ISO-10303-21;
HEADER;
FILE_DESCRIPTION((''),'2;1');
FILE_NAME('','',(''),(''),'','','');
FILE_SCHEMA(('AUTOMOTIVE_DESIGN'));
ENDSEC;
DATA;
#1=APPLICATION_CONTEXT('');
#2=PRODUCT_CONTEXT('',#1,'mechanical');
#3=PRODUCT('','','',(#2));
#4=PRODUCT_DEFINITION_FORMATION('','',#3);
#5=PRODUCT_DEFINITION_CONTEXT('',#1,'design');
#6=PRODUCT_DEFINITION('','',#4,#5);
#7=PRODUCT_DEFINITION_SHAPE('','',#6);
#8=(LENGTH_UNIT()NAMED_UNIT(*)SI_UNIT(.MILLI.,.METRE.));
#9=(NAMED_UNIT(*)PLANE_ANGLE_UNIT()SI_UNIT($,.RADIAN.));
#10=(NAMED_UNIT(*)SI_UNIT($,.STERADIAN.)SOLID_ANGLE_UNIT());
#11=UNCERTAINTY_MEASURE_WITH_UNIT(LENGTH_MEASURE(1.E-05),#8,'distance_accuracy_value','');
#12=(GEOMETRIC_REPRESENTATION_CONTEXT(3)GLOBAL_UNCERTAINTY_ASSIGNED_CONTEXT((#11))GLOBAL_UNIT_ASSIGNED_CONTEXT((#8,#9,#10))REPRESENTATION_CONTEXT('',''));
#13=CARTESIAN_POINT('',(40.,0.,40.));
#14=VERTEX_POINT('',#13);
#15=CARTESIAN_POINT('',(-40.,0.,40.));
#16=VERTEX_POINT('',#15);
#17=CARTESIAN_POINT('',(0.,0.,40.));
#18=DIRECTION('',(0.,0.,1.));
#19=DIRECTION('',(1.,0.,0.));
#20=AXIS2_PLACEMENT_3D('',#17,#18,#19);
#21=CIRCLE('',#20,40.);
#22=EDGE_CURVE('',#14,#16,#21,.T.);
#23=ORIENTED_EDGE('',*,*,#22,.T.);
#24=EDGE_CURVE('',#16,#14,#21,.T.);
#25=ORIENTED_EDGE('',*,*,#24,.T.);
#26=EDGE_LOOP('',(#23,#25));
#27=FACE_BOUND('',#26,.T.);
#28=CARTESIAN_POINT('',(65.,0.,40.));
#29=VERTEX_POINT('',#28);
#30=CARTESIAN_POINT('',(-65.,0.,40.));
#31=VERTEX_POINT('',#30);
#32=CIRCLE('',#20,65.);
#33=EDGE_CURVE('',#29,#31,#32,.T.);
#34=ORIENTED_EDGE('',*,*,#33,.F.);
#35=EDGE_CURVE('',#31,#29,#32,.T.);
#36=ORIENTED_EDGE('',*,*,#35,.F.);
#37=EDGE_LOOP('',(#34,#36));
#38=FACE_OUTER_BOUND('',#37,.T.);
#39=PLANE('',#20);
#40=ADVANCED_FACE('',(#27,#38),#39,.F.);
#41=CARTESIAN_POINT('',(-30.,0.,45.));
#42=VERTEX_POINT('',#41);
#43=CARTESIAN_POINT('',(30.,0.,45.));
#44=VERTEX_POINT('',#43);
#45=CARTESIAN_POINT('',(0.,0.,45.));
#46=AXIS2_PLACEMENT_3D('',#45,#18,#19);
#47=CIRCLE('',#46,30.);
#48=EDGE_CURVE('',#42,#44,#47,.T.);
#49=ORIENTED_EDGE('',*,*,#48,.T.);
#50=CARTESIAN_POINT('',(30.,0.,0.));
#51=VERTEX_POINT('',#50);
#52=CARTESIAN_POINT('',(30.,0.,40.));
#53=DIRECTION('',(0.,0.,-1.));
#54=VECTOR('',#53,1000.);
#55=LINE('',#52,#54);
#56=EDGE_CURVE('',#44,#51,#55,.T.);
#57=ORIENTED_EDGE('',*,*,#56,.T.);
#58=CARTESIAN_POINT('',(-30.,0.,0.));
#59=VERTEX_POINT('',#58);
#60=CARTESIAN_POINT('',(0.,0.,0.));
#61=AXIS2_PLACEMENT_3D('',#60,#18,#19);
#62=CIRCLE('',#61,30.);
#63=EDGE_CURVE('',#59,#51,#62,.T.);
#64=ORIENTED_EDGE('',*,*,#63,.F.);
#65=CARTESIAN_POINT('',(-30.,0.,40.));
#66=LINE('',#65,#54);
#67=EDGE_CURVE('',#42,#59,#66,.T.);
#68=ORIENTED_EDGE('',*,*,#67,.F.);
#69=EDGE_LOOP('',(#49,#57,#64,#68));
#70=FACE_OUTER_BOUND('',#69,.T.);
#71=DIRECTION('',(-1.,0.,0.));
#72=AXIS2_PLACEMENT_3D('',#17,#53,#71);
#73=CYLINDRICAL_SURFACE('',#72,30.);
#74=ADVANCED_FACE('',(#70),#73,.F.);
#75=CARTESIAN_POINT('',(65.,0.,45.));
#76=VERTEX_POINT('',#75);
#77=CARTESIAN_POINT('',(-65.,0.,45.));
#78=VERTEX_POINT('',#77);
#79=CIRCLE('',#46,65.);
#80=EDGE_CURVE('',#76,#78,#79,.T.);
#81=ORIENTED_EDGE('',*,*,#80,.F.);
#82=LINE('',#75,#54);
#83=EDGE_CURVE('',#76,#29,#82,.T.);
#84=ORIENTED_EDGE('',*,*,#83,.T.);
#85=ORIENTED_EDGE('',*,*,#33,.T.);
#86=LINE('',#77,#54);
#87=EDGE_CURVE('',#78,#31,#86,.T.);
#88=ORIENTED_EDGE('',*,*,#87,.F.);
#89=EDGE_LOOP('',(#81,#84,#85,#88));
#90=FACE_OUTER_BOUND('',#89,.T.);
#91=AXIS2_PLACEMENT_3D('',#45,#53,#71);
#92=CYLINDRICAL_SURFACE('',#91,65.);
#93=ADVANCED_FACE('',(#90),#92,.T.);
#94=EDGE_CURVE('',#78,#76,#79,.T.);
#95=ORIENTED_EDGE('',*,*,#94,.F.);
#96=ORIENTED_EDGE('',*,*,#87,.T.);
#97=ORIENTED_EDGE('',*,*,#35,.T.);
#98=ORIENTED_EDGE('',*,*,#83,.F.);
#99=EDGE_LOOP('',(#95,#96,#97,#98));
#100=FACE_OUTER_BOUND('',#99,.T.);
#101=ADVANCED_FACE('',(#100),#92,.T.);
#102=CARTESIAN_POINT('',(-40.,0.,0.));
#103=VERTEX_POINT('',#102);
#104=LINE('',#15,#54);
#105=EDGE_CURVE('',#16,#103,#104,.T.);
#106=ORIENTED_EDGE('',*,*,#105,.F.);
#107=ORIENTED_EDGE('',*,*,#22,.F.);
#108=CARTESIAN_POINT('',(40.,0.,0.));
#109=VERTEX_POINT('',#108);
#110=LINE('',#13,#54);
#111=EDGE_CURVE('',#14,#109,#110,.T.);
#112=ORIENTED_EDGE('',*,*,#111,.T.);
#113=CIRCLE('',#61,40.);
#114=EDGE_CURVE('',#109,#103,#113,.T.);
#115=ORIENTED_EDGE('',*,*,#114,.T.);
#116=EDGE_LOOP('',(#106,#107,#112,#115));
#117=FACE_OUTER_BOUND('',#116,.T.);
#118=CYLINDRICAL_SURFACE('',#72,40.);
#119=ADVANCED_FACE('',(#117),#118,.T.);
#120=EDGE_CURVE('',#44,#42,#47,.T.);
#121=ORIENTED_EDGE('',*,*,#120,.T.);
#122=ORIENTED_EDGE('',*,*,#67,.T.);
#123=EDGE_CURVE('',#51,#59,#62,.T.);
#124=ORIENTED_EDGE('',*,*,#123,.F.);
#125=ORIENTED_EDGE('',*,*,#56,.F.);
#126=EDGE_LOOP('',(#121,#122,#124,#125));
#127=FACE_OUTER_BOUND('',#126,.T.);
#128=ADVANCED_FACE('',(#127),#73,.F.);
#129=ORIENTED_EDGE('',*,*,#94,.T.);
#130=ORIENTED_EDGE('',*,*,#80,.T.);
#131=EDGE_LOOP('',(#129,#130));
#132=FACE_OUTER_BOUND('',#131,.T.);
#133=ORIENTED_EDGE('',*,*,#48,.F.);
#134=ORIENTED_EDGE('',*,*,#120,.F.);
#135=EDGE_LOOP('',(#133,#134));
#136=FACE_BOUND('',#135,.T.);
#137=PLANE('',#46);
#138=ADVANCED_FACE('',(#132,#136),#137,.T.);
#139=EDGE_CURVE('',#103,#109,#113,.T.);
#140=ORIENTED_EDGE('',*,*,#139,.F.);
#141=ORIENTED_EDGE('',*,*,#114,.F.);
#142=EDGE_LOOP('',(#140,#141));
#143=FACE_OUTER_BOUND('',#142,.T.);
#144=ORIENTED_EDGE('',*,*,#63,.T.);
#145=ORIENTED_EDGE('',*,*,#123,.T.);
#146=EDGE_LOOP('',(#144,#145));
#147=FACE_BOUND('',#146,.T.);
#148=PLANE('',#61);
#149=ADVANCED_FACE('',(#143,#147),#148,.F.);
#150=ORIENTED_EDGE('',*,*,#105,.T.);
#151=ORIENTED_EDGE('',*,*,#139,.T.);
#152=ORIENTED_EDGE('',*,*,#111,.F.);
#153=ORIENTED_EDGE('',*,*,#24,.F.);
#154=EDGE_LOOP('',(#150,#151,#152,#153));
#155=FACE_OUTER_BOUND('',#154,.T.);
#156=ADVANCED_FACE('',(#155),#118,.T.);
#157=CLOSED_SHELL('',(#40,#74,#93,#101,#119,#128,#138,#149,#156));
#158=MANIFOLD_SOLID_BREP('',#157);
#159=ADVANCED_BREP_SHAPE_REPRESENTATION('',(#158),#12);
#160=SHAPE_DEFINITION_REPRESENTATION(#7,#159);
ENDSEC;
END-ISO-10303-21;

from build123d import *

# Parameters (mm, degrees)
SKETCH1_R           = 40
SKETCH1_R_2         = 30
BOSS_EXTRUDE1_DEPTH = 40
SKETCH2_R           = 65
SKETCH2_R_2         = 30
BOSS_EXTRUDE2_DEPTH = 5


with BuildPart() as part:
    # Sketch1 → Boss-Extrude1 (new body)
    with BuildSketch(Plane.XY):
        Circle(SKETCH1_R)
        Circle(SKETCH1_R_2, mode=Mode.SUBTRACT)
    extrude(amount=BOSS_EXTRUDE1_DEPTH)

    # Sketch2 → Boss-Extrude2 (add)
    with BuildSketch(Plane.XY.offset(40)):
        Circle(SKETCH2_R)
        Circle(SKETCH2_R_2, mode=Mode.SUBTRACT)
    extrude(amount=BOSS_EXTRUDE2_DEPTH)


solid = part.part
